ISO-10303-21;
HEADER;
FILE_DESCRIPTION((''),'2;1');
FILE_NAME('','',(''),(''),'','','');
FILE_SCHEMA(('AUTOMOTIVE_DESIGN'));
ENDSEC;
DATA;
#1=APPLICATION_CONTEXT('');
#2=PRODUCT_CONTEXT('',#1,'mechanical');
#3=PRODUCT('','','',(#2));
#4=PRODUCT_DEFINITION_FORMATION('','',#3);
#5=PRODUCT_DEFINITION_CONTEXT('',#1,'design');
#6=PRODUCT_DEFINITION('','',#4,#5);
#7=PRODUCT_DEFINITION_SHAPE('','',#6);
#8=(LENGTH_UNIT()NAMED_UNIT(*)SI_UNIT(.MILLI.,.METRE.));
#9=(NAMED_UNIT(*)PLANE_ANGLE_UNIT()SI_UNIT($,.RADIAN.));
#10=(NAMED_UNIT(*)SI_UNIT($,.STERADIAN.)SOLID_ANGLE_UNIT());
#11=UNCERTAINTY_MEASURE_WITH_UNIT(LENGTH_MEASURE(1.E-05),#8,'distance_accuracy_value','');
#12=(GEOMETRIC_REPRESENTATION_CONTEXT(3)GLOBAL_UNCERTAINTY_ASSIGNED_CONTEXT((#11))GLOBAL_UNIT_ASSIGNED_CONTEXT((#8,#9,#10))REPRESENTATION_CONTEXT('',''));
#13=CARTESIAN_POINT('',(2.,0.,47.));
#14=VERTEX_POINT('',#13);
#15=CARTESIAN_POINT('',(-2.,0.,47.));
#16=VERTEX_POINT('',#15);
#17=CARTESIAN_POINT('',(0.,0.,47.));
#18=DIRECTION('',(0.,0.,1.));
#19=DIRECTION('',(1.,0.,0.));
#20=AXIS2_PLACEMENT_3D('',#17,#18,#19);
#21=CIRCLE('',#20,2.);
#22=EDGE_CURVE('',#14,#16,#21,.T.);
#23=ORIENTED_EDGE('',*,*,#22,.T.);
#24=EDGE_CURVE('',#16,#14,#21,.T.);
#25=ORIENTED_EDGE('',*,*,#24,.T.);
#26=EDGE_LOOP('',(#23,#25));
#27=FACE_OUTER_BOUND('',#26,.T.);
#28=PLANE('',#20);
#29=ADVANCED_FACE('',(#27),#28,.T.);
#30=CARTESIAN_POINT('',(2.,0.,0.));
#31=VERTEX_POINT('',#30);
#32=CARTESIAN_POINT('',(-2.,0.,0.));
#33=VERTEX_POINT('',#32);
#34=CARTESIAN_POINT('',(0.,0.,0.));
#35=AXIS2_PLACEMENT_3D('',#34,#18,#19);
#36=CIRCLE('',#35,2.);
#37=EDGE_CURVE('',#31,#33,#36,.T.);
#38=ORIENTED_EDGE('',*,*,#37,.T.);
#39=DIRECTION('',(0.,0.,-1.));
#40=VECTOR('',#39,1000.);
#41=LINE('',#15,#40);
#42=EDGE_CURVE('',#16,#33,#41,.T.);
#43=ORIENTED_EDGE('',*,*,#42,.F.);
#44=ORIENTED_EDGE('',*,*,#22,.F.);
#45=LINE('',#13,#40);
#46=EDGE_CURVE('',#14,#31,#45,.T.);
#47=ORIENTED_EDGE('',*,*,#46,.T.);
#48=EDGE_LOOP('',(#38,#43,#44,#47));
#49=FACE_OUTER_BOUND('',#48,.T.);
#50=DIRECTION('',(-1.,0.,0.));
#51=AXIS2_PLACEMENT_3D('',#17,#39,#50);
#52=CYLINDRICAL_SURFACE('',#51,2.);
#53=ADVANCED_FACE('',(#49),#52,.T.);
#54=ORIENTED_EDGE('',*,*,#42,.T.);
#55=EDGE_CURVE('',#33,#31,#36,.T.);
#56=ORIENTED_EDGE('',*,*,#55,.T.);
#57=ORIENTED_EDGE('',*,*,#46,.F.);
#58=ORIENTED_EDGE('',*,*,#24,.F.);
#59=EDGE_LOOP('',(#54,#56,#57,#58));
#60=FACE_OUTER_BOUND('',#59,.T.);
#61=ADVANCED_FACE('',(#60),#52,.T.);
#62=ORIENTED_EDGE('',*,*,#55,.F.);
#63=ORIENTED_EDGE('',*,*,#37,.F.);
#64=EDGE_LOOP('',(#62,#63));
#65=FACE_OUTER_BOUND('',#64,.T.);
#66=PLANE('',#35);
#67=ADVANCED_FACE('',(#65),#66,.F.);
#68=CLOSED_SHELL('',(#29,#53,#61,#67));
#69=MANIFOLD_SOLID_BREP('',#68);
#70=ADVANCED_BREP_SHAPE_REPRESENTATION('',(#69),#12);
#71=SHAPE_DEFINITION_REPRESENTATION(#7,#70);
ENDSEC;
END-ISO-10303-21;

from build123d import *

# Parameters (mm, degrees)
SKETCH_1_R      = 2
EXTRUDE_1_DEPTH = 47


with BuildPart() as part:
    # 草图1 → 凸台-拉伸1 (new body)
    with BuildSketch(Plane.XY):
        Circle(SKETCH_1_R)
    extrude(amount=EXTRUDE_1_DEPTH)


solid = part.part
